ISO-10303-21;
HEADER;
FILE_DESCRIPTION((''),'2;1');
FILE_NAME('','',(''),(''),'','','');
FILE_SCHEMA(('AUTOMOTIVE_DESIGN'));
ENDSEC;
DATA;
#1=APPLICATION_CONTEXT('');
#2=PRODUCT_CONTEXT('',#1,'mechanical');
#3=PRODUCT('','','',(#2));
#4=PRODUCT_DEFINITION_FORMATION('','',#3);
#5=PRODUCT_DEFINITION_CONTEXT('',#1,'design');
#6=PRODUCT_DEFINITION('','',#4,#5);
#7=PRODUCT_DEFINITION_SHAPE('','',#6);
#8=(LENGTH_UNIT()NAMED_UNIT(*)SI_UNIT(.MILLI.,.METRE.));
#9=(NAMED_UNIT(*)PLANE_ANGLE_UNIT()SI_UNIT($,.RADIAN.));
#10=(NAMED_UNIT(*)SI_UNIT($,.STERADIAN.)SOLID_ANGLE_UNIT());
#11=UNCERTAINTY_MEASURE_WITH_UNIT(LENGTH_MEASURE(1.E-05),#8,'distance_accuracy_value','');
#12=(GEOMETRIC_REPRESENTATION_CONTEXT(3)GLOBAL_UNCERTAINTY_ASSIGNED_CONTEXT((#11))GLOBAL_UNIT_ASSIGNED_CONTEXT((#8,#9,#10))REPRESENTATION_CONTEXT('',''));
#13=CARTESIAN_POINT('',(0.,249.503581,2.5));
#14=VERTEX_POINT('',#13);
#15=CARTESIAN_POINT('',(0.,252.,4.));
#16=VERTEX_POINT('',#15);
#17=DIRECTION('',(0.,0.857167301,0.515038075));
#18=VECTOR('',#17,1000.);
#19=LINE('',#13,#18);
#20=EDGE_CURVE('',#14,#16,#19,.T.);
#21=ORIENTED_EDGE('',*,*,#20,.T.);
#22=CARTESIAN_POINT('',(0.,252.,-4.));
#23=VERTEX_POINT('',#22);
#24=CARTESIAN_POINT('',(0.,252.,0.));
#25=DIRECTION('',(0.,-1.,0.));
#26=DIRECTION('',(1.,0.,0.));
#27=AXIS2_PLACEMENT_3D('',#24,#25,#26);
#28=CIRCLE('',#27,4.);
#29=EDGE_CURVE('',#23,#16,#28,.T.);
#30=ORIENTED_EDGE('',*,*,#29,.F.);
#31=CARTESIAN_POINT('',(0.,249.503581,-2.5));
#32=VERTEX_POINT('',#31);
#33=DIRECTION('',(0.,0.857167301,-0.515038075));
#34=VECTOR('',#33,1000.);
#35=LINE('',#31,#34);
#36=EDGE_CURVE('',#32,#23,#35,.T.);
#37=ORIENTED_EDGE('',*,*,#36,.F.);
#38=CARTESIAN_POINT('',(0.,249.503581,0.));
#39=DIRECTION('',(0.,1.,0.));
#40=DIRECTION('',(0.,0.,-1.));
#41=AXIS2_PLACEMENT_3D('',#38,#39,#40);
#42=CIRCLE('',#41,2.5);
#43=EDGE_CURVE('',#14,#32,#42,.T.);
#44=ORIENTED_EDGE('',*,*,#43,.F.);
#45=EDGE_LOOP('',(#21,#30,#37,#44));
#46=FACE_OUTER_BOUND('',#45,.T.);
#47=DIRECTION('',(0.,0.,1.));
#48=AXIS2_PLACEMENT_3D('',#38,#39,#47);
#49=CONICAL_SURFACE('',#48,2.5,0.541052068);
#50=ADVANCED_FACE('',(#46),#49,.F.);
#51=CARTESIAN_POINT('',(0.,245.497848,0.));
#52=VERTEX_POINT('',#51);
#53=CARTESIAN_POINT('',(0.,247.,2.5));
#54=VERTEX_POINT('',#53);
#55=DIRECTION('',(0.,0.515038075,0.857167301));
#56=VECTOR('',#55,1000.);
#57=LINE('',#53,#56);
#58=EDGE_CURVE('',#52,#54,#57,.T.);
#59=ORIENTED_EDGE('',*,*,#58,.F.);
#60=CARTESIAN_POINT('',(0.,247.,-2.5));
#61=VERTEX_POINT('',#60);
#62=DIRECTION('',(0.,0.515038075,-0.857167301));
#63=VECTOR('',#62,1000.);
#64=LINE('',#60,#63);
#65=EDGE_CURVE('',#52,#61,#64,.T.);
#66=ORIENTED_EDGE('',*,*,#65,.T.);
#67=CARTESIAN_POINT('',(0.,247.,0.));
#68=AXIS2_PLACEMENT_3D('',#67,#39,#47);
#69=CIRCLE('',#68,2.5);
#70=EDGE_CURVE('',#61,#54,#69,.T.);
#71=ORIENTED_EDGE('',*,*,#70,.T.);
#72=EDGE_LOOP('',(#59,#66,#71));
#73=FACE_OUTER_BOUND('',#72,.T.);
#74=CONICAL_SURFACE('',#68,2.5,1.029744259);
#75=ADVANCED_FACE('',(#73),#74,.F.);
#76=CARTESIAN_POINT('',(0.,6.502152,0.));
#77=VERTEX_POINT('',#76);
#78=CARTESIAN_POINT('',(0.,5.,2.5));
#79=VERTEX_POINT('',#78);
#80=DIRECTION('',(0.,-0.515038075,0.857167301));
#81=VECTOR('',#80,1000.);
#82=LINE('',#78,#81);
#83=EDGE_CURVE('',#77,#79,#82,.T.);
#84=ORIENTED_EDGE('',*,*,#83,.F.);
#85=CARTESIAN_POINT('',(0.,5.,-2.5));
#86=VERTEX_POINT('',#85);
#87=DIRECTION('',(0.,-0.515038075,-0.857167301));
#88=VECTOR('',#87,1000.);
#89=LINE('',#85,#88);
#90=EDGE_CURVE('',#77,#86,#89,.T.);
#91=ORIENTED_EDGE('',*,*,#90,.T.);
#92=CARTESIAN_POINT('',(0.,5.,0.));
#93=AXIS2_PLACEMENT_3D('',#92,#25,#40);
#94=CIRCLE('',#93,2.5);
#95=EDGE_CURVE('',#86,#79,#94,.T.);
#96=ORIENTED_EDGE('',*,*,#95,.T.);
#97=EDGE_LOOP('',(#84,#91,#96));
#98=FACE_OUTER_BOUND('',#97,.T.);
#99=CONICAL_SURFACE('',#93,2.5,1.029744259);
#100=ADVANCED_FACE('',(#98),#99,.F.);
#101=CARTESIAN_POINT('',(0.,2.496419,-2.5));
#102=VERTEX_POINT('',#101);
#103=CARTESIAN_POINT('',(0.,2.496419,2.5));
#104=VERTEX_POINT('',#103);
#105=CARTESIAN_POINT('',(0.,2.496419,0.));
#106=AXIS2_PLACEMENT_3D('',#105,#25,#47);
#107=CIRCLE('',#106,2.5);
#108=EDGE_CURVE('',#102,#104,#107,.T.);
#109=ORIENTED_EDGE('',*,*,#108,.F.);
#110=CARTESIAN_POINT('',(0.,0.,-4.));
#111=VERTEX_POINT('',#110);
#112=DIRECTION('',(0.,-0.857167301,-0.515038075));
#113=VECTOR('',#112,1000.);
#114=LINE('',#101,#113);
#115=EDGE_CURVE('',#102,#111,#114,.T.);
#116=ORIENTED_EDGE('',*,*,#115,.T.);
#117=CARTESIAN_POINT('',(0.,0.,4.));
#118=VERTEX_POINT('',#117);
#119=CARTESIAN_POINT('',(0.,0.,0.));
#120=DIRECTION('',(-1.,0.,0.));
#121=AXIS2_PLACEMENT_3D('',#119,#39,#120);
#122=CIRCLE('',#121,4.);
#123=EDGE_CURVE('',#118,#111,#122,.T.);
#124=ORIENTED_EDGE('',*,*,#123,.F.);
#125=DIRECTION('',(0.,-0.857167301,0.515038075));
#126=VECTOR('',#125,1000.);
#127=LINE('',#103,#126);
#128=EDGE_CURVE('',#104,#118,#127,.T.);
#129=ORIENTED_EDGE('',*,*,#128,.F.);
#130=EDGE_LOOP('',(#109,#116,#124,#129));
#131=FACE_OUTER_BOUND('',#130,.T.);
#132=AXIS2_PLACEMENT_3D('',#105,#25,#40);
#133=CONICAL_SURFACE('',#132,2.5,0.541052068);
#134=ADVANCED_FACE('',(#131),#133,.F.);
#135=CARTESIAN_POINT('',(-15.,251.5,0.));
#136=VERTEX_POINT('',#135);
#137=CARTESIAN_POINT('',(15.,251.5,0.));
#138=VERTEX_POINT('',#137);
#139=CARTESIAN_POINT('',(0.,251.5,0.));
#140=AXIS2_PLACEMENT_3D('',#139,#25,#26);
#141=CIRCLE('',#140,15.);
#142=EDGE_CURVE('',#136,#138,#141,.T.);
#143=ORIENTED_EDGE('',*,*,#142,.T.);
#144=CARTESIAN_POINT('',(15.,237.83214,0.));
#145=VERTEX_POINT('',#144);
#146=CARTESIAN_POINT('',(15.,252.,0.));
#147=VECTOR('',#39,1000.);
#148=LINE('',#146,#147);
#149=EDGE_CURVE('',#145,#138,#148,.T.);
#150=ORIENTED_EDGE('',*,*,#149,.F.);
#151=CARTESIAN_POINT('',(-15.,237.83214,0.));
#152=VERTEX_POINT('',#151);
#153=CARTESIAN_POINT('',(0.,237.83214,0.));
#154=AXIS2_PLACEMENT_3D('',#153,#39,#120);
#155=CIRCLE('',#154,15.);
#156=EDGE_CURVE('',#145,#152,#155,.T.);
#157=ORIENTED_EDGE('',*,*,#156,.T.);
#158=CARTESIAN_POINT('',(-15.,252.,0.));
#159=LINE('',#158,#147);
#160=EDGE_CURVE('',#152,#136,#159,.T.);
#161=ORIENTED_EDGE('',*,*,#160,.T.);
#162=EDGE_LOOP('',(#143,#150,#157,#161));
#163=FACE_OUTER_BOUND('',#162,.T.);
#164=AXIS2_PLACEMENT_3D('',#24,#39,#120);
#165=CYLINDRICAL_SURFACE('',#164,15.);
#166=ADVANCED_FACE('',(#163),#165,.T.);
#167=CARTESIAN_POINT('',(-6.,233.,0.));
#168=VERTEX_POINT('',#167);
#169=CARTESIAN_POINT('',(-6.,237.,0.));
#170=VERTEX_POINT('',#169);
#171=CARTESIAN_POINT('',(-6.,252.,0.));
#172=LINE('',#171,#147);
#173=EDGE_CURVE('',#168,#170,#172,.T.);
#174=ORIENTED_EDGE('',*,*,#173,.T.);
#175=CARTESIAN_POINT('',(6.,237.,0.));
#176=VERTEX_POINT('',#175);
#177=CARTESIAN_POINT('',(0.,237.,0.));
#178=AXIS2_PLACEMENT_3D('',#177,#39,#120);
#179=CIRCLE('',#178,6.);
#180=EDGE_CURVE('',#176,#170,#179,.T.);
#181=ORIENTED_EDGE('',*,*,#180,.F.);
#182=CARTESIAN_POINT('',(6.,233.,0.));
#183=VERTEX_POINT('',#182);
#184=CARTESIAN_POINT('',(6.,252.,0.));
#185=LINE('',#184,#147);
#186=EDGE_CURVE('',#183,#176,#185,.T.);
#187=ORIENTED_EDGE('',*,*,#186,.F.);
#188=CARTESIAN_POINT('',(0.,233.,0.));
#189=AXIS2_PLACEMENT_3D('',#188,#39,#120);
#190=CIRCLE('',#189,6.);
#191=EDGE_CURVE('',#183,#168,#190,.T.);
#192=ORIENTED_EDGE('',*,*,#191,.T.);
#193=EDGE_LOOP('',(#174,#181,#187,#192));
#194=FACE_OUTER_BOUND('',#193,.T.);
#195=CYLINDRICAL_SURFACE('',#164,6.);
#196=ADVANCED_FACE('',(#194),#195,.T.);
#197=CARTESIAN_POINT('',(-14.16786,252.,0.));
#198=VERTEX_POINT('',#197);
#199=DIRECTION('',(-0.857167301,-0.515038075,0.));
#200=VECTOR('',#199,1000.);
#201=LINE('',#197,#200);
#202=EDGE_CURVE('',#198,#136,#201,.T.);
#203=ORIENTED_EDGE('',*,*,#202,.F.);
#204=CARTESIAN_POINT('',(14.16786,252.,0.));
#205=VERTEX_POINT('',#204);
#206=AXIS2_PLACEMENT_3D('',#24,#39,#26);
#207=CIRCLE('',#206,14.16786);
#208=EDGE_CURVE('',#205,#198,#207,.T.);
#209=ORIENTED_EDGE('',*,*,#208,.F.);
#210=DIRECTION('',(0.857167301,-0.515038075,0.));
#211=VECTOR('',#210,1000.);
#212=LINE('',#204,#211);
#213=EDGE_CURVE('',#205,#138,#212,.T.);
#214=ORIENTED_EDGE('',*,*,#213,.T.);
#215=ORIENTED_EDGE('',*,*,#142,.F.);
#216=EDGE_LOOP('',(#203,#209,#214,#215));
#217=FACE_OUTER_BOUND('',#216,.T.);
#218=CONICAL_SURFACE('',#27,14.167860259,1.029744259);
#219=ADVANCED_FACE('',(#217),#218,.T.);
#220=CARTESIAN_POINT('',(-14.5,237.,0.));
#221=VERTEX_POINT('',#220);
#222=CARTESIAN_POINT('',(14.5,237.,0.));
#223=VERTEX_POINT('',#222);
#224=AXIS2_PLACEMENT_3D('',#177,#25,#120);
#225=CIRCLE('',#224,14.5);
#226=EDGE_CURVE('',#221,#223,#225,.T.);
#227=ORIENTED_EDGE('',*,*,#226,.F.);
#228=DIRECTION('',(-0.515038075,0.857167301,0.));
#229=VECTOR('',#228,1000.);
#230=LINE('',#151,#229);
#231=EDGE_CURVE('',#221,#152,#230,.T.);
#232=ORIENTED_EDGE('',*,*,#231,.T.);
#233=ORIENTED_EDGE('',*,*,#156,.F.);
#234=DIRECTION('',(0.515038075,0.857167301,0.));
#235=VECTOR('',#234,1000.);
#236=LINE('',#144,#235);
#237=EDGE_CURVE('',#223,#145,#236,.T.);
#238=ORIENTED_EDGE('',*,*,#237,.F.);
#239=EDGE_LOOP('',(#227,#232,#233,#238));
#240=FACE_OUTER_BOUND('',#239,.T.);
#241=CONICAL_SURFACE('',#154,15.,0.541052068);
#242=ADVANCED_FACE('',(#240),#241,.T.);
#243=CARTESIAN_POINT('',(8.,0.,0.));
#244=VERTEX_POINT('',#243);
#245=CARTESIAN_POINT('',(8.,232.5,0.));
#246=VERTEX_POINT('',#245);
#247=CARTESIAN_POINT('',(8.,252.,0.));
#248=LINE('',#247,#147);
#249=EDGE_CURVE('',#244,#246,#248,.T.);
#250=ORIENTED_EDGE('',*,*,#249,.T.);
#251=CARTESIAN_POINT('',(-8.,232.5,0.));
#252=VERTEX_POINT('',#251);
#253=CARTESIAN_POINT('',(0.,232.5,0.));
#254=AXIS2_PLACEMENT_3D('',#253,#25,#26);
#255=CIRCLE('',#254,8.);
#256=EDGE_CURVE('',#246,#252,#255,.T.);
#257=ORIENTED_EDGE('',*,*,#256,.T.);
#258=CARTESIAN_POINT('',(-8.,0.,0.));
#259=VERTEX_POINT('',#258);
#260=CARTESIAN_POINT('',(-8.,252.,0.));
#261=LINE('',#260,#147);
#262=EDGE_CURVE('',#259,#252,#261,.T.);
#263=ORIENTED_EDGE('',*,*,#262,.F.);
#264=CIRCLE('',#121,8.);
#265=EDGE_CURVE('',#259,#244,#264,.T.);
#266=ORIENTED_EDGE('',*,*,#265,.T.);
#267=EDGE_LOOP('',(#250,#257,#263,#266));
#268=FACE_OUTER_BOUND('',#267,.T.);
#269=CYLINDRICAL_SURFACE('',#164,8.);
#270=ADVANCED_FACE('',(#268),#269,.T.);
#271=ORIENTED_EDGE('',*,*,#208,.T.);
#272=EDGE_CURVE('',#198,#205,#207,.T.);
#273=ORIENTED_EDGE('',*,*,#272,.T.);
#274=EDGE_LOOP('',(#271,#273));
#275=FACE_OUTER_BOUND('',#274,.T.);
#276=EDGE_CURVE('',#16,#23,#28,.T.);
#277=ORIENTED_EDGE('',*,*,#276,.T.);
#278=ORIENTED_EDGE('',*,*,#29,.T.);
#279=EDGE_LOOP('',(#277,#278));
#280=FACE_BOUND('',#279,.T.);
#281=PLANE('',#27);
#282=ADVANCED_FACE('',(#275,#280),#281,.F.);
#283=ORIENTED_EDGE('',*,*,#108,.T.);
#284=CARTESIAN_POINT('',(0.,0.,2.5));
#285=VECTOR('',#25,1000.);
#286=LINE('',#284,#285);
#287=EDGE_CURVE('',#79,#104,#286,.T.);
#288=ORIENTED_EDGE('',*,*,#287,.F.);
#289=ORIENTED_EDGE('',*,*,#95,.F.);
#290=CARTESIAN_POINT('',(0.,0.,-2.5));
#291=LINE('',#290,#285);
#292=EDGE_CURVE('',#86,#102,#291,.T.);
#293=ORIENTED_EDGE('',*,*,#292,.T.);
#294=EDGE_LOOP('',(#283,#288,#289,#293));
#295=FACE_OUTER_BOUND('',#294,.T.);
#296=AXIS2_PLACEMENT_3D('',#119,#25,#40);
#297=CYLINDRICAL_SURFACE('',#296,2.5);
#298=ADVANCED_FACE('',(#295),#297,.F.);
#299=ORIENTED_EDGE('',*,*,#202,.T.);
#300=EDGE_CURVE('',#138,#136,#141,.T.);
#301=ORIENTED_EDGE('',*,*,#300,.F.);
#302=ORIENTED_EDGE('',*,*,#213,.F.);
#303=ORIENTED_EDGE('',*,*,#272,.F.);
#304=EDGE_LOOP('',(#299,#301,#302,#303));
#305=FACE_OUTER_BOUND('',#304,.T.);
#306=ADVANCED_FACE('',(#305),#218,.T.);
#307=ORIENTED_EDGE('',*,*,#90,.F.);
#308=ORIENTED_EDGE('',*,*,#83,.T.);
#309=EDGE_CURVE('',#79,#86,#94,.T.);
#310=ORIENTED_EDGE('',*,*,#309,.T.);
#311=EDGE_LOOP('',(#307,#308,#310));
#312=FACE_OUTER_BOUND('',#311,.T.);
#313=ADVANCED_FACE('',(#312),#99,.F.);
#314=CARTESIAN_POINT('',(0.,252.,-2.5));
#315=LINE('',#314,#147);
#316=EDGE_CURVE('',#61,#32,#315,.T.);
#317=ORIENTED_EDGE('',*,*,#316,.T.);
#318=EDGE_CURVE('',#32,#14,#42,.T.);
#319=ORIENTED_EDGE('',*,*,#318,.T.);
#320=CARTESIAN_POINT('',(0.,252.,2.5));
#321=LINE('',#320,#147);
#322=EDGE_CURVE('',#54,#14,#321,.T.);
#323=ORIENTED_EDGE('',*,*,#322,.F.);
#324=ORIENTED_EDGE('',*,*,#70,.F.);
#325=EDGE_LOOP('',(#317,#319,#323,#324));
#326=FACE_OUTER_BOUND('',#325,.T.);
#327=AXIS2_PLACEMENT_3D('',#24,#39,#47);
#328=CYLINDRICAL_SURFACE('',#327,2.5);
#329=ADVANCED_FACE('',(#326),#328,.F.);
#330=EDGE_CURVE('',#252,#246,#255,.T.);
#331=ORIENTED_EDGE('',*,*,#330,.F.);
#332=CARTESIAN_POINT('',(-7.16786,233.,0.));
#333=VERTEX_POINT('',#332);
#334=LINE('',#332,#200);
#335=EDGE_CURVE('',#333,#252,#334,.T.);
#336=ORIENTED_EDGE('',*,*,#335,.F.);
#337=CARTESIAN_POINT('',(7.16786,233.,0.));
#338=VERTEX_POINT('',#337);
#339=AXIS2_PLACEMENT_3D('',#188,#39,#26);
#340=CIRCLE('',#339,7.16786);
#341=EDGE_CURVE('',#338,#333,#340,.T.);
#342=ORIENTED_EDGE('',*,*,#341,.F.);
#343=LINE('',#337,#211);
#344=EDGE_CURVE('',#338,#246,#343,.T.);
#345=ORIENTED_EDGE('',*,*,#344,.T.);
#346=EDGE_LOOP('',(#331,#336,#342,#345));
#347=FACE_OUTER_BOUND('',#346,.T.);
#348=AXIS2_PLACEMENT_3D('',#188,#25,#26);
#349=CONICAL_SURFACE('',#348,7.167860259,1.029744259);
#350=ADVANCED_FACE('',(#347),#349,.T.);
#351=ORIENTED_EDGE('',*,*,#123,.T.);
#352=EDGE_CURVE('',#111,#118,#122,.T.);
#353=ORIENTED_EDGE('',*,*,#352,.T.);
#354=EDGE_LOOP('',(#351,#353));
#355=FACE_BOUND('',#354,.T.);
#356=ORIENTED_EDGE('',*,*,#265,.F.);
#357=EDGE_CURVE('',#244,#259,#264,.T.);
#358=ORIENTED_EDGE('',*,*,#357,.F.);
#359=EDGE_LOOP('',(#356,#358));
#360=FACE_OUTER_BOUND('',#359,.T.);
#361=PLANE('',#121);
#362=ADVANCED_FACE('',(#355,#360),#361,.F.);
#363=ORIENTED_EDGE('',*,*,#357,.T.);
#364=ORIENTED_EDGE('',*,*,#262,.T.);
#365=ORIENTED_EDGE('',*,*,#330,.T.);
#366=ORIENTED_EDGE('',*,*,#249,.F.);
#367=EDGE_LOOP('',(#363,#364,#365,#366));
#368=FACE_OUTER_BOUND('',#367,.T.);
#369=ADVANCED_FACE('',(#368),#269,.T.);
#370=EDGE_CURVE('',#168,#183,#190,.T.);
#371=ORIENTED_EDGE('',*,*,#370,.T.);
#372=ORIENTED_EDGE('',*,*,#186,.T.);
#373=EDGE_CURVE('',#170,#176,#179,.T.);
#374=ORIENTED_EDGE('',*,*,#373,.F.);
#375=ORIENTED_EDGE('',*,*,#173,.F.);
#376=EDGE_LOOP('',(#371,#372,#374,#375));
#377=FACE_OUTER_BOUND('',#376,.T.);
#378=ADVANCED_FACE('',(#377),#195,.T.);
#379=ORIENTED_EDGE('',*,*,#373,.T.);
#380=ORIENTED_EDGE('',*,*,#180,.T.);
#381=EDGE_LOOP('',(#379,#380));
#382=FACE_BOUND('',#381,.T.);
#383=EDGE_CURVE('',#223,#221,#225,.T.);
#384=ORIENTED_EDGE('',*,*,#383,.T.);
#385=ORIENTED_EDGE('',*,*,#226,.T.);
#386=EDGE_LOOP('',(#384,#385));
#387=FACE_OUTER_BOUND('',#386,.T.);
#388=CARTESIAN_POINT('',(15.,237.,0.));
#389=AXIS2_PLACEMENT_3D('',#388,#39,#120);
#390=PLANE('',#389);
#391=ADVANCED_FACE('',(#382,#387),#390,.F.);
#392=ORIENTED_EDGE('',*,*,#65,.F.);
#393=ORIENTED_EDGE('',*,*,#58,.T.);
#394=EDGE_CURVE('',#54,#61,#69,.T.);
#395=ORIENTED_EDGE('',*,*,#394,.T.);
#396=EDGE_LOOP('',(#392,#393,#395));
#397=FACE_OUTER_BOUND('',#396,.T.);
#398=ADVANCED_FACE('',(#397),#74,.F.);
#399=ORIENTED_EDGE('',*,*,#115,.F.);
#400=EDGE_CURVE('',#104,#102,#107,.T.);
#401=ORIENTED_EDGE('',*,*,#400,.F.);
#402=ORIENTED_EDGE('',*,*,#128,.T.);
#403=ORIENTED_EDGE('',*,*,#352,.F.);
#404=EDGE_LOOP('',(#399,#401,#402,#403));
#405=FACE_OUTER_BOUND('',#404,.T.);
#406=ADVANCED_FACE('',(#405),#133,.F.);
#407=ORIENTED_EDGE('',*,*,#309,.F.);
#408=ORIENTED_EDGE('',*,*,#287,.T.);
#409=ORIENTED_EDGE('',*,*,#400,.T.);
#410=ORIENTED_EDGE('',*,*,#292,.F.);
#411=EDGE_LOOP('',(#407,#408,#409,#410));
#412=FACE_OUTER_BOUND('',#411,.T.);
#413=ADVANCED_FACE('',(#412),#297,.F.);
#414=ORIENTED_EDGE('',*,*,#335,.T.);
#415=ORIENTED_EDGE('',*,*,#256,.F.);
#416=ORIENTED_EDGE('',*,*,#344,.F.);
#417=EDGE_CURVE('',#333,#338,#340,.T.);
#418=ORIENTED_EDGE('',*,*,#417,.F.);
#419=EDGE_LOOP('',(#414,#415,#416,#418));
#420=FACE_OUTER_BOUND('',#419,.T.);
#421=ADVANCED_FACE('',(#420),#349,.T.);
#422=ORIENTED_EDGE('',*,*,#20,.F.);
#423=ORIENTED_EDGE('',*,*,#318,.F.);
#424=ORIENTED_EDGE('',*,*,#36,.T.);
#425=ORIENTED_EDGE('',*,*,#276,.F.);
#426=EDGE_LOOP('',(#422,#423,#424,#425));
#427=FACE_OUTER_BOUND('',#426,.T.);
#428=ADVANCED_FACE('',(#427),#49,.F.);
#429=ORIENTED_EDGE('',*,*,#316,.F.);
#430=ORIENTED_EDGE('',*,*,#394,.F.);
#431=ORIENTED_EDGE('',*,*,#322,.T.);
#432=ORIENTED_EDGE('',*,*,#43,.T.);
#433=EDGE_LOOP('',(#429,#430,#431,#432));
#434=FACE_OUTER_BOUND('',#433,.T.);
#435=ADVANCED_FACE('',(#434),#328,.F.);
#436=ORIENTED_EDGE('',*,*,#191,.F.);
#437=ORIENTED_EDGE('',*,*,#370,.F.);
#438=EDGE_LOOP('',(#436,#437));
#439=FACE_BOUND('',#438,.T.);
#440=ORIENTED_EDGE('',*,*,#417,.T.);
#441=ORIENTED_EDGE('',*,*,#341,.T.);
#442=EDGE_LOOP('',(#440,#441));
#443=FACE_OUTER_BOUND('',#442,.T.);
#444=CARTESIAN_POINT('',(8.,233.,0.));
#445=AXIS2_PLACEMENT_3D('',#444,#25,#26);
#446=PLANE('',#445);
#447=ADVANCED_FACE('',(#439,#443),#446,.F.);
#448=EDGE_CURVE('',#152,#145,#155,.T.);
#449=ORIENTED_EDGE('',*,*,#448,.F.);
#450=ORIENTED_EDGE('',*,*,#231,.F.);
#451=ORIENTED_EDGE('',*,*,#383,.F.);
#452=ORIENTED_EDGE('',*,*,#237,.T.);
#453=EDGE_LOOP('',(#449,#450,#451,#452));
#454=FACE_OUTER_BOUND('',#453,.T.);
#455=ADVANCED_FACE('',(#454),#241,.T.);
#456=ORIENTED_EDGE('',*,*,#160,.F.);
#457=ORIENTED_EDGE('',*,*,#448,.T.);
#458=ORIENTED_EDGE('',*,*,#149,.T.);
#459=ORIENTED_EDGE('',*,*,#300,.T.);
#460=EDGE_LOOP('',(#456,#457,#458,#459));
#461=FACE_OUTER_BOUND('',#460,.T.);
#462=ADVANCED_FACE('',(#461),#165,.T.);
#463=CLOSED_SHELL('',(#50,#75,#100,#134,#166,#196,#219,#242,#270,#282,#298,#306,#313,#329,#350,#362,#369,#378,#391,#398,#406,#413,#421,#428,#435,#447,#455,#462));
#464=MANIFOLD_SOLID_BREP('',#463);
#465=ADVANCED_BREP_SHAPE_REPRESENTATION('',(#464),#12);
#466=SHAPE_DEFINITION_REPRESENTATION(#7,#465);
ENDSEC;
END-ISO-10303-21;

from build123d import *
from OCP.BRepFilletAPI import BRepFilletAPI_MakeChamfer

# Parameters (mm, degrees)
F_5_0MM_DOWEL_HOLE1_D     = 5
F_5_0MM_DOWEL_HOLE1_DEPTH = 5
F_5_0MM_DOWEL_HOLE1_TIP   = 1.502151548
CHAMFER1_SIZE             = 1.5
CHAMFER1_SIZE2            = 2.496419224
CHAMFER2_SIZE             = 0.5
CHAMFER2_SIZE2            = 0.832139741
F_5_0MM_DOWEL_HOLE2_D     = 5
F_5_0MM_DOWEL_HOLE2_DEPTH = 5
F_5_0MM_DOWEL_HOLE2_TIP   = 1.502151548
CHAMFER3_SIZE             = 1.5
CHAMFER3_SIZE2            = 2.496419224


with BuildPart() as part:
    # Sketch1 → Revolve1 (revolve)
    with BuildSketch(Plane.XY, mode=Mode.PRIVATE) as revolve1_sk:
        Polygon((0, 252), (15, 252), (15, 237), (6, 237), (6, 233), (8, 233), (8, 0), (0, 0), align=None)
    revolve(revolve1_sk.sketch.rotate(Axis((0, 252, 0), (0, -1, 0)), 180), axis=Axis((0, 252, 0), (0, -1, 0)))

    # Ø5.0mm Dowel Hole1
    with Locations(Plane(origin=(0, 0, 0), x_dir=(-1, 0, 0), z_dir=(0, -1, 0))):
        with Locations((0, 0), (163.193456079, -92.802944279)):
            Hole(F_5_0MM_DOWEL_HOLE1_D / 2, depth=F_5_0MM_DOWEL_HOLE1_DEPTH)
            with Locations((0, 0, -(F_5_0MM_DOWEL_HOLE1_DEPTH + F_5_0MM_DOWEL_HOLE1_TIP / 2))):  # 118° drill point
                Cone(0, F_5_0MM_DOWEL_HOLE1_D / 2, F_5_0MM_DOWEL_HOLE1_TIP, mode=Mode.SUBTRACT)

    # Chamfer1
    chamfer1_edges = [part.edges().sort_by_distance(p)[0] for p in [
        (-2.5, 0, 0),
    ]]
    chamfer1_side = [part.faces().sort_by_distance(p)[0] for p in [
        (7.77372583, 0, 0),
    ]]
    chamfer(chamfer1_edges, length=CHAMFER1_SIZE, length2=CHAMFER1_SIZE2, reference=chamfer1_side[0])

    # Chamfer2: one chamfer whose edges measure the first distance from different faces: ONE call of the kernel's chamfer builder (chamfer() names one face for all edges)
    chamfer2_edges_1 = [part.edges().sort_by_distance(p)[0] for p in [
        (15, 237, 0),
    ]]
    chamfer2_side_1 = [part.faces().sort_by_distance(p)[0] for p in [
        (14.575735931, 237, 0),
    ]]
    chamfer2_edges_2 = [part.edges().sort_by_distance(p)[0] for p in [
        (15, 252, 0),
    ]]
    chamfer2_side_2 = [part.faces().sort_by_distance(p)[0] for p in [
        (15, 244.5, 0),
    ]]
    chamfer2_edges_3 = [part.edges().sort_by_distance(p)[0] for p in [
        (8, 233, 0),
    ]]
    chamfer2_side_3 = [part.faces().sort_by_distance(p)[0] for p in [
        (8, 116.5, 0),
    ]]
    chamfer2 = BRepFilletAPI_MakeChamfer(part.part.solid().wrapped)
    for e in chamfer2_edges_1:
        chamfer2.Add(CHAMFER2_SIZE, CHAMFER2_SIZE2, e.wrapped, chamfer2_side_1[0].wrapped)  # the first distance lies on this face
    for e in chamfer2_edges_2:
        chamfer2.Add(CHAMFER2_SIZE, CHAMFER2_SIZE2, e.wrapped, chamfer2_side_2[0].wrapped)  # the first distance lies on this face
    for e in chamfer2_edges_3:
        chamfer2.Add(CHAMFER2_SIZE, CHAMFER2_SIZE2, e.wrapped, chamfer2_side_3[0].wrapped)  # the first distance lies on this face
    add(Compound.cast(chamfer2.Shape()), mode=Mode.REPLACE)

    # Ø5.0mm Dowel Hole2
    with Locations(Plane(origin=(0, 252, 0), x_dir=(1, 0, 0), z_dir=(0, 1, 0))):
        with Locations((0, 0)):
            Hole(F_5_0MM_DOWEL_HOLE2_D / 2, depth=F_5_0MM_DOWEL_HOLE2_DEPTH)
            with Locations((0, 0, -(F_5_0MM_DOWEL_HOLE2_DEPTH + F_5_0MM_DOWEL_HOLE2_TIP / 2))):  # 118° drill point
                Cone(0, F_5_0MM_DOWEL_HOLE2_D / 2, F_5_0MM_DOWEL_HOLE2_TIP, mode=Mode.SUBTRACT)

    # Chamfer3
    chamfer3_edges = [part.edges().sort_by_distance(p)[0] for p in [
        (2.5, 252, 0),
    ]]
    chamfer3_side = [part.faces().sort_by_distance(p)[0] for p in [
        (13.767132656, 252, 0),
    ]]
    chamfer(chamfer3_edges, length=CHAMFER3_SIZE, length2=CHAMFER3_SIZE2, reference=chamfer3_side[0])


solid = part.part
